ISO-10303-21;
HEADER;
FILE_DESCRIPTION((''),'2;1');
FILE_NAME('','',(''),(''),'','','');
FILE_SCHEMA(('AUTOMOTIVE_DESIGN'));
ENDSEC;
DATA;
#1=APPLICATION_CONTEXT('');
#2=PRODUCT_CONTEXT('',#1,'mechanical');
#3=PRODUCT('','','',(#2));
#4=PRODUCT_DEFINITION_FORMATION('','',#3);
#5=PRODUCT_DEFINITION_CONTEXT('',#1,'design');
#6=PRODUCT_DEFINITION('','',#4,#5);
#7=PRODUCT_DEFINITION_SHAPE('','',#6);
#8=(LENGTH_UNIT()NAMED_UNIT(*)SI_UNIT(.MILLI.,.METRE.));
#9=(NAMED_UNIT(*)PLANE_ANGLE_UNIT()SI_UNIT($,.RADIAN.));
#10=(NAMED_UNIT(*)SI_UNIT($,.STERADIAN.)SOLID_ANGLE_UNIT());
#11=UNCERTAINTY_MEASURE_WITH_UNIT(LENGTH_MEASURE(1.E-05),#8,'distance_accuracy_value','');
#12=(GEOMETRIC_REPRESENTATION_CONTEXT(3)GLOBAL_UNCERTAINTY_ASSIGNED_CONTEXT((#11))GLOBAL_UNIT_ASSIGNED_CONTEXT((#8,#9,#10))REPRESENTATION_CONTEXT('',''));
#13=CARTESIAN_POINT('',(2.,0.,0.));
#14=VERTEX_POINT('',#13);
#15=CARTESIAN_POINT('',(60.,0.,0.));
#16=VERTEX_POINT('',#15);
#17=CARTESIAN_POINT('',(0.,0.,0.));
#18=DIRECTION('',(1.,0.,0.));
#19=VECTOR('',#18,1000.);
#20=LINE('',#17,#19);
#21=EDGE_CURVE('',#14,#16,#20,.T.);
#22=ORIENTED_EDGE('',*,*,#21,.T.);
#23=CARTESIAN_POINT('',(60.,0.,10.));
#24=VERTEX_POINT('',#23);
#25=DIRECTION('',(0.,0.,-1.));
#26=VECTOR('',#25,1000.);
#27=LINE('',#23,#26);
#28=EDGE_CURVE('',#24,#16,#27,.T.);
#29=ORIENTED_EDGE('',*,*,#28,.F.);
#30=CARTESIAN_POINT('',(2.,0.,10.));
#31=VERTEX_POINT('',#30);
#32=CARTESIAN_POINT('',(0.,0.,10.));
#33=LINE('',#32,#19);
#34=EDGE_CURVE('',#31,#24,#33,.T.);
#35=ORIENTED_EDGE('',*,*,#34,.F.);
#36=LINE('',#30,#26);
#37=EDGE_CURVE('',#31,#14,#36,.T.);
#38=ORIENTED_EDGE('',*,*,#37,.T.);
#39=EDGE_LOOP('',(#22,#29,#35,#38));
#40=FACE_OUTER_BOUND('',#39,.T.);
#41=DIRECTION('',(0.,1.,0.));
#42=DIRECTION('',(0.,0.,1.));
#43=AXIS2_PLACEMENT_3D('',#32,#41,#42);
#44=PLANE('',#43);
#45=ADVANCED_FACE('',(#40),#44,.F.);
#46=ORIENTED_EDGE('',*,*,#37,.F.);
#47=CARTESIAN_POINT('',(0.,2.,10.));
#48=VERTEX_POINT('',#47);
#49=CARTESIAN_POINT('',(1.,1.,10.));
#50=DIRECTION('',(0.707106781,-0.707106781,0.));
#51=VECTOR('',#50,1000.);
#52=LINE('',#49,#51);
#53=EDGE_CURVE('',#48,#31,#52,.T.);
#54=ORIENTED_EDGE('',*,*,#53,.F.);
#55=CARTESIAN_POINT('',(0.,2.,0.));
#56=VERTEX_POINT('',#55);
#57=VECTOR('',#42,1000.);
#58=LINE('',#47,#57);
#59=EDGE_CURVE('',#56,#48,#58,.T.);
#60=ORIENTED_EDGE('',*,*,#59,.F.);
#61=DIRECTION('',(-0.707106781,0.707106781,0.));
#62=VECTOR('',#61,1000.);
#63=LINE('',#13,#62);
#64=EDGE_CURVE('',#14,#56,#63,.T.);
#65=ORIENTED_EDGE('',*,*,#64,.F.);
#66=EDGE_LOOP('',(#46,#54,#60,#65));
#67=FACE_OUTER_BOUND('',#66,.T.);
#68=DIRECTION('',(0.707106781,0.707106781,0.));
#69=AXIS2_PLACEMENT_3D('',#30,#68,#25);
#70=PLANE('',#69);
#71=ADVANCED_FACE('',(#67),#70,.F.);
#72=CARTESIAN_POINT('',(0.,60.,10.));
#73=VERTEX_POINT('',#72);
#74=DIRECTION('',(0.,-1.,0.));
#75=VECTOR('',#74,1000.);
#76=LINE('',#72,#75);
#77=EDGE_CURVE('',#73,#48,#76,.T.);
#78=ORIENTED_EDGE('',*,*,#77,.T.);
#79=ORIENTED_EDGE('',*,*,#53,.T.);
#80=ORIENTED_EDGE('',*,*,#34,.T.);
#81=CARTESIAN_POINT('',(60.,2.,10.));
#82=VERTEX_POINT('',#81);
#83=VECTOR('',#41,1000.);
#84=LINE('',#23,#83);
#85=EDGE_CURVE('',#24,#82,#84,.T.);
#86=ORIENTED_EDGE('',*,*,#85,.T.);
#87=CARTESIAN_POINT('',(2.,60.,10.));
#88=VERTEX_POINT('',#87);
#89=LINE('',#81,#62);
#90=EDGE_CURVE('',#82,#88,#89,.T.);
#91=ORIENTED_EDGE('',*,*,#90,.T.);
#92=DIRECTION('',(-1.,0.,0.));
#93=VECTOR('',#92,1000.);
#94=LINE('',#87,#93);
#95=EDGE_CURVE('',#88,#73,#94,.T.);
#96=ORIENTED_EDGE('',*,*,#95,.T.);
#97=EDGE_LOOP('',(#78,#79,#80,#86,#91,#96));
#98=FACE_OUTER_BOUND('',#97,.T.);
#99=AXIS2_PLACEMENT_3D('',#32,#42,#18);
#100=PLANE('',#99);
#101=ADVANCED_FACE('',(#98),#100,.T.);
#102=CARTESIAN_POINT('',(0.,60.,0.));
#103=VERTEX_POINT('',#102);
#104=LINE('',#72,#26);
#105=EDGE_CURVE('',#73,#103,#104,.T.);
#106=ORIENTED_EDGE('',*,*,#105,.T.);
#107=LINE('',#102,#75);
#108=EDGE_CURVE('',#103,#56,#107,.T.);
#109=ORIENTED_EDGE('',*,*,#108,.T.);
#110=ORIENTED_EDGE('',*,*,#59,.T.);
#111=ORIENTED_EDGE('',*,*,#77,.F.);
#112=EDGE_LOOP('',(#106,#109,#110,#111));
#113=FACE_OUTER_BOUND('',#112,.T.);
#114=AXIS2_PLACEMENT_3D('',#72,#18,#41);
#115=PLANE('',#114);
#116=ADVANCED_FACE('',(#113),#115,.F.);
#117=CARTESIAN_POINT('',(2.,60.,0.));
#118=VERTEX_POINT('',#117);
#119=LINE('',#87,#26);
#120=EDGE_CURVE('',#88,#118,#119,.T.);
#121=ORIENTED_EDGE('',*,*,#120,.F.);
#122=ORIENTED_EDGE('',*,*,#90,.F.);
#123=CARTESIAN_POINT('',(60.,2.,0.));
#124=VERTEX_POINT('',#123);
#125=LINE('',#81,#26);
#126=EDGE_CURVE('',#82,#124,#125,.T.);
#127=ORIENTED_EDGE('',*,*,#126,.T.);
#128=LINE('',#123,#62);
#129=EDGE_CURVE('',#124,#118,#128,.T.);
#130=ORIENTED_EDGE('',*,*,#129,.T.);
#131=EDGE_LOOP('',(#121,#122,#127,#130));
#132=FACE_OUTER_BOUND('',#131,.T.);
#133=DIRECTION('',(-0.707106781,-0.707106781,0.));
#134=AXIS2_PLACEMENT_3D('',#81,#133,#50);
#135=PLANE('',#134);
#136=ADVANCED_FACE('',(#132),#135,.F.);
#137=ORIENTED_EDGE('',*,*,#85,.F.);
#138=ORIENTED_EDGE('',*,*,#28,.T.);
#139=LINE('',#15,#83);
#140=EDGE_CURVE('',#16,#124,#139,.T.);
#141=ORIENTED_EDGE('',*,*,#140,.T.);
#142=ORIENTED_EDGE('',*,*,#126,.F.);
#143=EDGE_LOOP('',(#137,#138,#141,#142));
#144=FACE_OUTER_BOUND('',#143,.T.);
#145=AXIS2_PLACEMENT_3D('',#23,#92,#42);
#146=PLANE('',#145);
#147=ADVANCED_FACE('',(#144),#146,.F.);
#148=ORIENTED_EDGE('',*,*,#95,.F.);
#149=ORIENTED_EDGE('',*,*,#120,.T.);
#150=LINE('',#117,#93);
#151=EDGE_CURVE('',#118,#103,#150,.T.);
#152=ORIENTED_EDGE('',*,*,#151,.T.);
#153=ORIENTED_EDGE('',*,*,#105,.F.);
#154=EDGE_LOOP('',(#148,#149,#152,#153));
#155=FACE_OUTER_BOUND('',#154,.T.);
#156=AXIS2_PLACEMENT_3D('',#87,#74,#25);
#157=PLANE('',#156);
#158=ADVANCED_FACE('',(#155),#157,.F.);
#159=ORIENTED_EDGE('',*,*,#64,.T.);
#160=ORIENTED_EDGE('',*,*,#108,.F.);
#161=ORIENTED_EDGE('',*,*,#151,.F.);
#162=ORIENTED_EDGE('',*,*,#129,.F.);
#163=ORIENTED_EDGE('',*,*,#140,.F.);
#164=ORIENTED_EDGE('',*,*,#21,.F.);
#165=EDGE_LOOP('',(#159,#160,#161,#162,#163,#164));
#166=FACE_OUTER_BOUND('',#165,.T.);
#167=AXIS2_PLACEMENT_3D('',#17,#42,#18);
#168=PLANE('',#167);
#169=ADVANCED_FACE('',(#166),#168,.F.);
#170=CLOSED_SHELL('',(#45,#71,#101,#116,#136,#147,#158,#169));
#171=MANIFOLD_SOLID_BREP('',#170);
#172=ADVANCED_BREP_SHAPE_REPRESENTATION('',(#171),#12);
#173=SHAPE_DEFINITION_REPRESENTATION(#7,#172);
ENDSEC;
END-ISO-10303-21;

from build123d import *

# Parameters (mm, degrees)
BOSS_EXTRUDE1_DEPTH = 10
CHAMFER1_SIZE       = 2


with BuildPart() as part:
    # Sketch1 → Boss-Extrude1 (new body)
    with BuildSketch(Plane.XY):
        Polygon((0, 60), (0, 0), (60, 0), (60, 2), (2, 60), align=None)
    extrude(amount=BOSS_EXTRUDE1_DEPTH)

    # Chamfer1
    chamfer1_edges = [part.edges().sort_by_distance(p)[0] for p in [
        (0, 0, 5),
    ]]
    chamfer(chamfer1_edges, length=CHAMFER1_SIZE)


solid = part.part
